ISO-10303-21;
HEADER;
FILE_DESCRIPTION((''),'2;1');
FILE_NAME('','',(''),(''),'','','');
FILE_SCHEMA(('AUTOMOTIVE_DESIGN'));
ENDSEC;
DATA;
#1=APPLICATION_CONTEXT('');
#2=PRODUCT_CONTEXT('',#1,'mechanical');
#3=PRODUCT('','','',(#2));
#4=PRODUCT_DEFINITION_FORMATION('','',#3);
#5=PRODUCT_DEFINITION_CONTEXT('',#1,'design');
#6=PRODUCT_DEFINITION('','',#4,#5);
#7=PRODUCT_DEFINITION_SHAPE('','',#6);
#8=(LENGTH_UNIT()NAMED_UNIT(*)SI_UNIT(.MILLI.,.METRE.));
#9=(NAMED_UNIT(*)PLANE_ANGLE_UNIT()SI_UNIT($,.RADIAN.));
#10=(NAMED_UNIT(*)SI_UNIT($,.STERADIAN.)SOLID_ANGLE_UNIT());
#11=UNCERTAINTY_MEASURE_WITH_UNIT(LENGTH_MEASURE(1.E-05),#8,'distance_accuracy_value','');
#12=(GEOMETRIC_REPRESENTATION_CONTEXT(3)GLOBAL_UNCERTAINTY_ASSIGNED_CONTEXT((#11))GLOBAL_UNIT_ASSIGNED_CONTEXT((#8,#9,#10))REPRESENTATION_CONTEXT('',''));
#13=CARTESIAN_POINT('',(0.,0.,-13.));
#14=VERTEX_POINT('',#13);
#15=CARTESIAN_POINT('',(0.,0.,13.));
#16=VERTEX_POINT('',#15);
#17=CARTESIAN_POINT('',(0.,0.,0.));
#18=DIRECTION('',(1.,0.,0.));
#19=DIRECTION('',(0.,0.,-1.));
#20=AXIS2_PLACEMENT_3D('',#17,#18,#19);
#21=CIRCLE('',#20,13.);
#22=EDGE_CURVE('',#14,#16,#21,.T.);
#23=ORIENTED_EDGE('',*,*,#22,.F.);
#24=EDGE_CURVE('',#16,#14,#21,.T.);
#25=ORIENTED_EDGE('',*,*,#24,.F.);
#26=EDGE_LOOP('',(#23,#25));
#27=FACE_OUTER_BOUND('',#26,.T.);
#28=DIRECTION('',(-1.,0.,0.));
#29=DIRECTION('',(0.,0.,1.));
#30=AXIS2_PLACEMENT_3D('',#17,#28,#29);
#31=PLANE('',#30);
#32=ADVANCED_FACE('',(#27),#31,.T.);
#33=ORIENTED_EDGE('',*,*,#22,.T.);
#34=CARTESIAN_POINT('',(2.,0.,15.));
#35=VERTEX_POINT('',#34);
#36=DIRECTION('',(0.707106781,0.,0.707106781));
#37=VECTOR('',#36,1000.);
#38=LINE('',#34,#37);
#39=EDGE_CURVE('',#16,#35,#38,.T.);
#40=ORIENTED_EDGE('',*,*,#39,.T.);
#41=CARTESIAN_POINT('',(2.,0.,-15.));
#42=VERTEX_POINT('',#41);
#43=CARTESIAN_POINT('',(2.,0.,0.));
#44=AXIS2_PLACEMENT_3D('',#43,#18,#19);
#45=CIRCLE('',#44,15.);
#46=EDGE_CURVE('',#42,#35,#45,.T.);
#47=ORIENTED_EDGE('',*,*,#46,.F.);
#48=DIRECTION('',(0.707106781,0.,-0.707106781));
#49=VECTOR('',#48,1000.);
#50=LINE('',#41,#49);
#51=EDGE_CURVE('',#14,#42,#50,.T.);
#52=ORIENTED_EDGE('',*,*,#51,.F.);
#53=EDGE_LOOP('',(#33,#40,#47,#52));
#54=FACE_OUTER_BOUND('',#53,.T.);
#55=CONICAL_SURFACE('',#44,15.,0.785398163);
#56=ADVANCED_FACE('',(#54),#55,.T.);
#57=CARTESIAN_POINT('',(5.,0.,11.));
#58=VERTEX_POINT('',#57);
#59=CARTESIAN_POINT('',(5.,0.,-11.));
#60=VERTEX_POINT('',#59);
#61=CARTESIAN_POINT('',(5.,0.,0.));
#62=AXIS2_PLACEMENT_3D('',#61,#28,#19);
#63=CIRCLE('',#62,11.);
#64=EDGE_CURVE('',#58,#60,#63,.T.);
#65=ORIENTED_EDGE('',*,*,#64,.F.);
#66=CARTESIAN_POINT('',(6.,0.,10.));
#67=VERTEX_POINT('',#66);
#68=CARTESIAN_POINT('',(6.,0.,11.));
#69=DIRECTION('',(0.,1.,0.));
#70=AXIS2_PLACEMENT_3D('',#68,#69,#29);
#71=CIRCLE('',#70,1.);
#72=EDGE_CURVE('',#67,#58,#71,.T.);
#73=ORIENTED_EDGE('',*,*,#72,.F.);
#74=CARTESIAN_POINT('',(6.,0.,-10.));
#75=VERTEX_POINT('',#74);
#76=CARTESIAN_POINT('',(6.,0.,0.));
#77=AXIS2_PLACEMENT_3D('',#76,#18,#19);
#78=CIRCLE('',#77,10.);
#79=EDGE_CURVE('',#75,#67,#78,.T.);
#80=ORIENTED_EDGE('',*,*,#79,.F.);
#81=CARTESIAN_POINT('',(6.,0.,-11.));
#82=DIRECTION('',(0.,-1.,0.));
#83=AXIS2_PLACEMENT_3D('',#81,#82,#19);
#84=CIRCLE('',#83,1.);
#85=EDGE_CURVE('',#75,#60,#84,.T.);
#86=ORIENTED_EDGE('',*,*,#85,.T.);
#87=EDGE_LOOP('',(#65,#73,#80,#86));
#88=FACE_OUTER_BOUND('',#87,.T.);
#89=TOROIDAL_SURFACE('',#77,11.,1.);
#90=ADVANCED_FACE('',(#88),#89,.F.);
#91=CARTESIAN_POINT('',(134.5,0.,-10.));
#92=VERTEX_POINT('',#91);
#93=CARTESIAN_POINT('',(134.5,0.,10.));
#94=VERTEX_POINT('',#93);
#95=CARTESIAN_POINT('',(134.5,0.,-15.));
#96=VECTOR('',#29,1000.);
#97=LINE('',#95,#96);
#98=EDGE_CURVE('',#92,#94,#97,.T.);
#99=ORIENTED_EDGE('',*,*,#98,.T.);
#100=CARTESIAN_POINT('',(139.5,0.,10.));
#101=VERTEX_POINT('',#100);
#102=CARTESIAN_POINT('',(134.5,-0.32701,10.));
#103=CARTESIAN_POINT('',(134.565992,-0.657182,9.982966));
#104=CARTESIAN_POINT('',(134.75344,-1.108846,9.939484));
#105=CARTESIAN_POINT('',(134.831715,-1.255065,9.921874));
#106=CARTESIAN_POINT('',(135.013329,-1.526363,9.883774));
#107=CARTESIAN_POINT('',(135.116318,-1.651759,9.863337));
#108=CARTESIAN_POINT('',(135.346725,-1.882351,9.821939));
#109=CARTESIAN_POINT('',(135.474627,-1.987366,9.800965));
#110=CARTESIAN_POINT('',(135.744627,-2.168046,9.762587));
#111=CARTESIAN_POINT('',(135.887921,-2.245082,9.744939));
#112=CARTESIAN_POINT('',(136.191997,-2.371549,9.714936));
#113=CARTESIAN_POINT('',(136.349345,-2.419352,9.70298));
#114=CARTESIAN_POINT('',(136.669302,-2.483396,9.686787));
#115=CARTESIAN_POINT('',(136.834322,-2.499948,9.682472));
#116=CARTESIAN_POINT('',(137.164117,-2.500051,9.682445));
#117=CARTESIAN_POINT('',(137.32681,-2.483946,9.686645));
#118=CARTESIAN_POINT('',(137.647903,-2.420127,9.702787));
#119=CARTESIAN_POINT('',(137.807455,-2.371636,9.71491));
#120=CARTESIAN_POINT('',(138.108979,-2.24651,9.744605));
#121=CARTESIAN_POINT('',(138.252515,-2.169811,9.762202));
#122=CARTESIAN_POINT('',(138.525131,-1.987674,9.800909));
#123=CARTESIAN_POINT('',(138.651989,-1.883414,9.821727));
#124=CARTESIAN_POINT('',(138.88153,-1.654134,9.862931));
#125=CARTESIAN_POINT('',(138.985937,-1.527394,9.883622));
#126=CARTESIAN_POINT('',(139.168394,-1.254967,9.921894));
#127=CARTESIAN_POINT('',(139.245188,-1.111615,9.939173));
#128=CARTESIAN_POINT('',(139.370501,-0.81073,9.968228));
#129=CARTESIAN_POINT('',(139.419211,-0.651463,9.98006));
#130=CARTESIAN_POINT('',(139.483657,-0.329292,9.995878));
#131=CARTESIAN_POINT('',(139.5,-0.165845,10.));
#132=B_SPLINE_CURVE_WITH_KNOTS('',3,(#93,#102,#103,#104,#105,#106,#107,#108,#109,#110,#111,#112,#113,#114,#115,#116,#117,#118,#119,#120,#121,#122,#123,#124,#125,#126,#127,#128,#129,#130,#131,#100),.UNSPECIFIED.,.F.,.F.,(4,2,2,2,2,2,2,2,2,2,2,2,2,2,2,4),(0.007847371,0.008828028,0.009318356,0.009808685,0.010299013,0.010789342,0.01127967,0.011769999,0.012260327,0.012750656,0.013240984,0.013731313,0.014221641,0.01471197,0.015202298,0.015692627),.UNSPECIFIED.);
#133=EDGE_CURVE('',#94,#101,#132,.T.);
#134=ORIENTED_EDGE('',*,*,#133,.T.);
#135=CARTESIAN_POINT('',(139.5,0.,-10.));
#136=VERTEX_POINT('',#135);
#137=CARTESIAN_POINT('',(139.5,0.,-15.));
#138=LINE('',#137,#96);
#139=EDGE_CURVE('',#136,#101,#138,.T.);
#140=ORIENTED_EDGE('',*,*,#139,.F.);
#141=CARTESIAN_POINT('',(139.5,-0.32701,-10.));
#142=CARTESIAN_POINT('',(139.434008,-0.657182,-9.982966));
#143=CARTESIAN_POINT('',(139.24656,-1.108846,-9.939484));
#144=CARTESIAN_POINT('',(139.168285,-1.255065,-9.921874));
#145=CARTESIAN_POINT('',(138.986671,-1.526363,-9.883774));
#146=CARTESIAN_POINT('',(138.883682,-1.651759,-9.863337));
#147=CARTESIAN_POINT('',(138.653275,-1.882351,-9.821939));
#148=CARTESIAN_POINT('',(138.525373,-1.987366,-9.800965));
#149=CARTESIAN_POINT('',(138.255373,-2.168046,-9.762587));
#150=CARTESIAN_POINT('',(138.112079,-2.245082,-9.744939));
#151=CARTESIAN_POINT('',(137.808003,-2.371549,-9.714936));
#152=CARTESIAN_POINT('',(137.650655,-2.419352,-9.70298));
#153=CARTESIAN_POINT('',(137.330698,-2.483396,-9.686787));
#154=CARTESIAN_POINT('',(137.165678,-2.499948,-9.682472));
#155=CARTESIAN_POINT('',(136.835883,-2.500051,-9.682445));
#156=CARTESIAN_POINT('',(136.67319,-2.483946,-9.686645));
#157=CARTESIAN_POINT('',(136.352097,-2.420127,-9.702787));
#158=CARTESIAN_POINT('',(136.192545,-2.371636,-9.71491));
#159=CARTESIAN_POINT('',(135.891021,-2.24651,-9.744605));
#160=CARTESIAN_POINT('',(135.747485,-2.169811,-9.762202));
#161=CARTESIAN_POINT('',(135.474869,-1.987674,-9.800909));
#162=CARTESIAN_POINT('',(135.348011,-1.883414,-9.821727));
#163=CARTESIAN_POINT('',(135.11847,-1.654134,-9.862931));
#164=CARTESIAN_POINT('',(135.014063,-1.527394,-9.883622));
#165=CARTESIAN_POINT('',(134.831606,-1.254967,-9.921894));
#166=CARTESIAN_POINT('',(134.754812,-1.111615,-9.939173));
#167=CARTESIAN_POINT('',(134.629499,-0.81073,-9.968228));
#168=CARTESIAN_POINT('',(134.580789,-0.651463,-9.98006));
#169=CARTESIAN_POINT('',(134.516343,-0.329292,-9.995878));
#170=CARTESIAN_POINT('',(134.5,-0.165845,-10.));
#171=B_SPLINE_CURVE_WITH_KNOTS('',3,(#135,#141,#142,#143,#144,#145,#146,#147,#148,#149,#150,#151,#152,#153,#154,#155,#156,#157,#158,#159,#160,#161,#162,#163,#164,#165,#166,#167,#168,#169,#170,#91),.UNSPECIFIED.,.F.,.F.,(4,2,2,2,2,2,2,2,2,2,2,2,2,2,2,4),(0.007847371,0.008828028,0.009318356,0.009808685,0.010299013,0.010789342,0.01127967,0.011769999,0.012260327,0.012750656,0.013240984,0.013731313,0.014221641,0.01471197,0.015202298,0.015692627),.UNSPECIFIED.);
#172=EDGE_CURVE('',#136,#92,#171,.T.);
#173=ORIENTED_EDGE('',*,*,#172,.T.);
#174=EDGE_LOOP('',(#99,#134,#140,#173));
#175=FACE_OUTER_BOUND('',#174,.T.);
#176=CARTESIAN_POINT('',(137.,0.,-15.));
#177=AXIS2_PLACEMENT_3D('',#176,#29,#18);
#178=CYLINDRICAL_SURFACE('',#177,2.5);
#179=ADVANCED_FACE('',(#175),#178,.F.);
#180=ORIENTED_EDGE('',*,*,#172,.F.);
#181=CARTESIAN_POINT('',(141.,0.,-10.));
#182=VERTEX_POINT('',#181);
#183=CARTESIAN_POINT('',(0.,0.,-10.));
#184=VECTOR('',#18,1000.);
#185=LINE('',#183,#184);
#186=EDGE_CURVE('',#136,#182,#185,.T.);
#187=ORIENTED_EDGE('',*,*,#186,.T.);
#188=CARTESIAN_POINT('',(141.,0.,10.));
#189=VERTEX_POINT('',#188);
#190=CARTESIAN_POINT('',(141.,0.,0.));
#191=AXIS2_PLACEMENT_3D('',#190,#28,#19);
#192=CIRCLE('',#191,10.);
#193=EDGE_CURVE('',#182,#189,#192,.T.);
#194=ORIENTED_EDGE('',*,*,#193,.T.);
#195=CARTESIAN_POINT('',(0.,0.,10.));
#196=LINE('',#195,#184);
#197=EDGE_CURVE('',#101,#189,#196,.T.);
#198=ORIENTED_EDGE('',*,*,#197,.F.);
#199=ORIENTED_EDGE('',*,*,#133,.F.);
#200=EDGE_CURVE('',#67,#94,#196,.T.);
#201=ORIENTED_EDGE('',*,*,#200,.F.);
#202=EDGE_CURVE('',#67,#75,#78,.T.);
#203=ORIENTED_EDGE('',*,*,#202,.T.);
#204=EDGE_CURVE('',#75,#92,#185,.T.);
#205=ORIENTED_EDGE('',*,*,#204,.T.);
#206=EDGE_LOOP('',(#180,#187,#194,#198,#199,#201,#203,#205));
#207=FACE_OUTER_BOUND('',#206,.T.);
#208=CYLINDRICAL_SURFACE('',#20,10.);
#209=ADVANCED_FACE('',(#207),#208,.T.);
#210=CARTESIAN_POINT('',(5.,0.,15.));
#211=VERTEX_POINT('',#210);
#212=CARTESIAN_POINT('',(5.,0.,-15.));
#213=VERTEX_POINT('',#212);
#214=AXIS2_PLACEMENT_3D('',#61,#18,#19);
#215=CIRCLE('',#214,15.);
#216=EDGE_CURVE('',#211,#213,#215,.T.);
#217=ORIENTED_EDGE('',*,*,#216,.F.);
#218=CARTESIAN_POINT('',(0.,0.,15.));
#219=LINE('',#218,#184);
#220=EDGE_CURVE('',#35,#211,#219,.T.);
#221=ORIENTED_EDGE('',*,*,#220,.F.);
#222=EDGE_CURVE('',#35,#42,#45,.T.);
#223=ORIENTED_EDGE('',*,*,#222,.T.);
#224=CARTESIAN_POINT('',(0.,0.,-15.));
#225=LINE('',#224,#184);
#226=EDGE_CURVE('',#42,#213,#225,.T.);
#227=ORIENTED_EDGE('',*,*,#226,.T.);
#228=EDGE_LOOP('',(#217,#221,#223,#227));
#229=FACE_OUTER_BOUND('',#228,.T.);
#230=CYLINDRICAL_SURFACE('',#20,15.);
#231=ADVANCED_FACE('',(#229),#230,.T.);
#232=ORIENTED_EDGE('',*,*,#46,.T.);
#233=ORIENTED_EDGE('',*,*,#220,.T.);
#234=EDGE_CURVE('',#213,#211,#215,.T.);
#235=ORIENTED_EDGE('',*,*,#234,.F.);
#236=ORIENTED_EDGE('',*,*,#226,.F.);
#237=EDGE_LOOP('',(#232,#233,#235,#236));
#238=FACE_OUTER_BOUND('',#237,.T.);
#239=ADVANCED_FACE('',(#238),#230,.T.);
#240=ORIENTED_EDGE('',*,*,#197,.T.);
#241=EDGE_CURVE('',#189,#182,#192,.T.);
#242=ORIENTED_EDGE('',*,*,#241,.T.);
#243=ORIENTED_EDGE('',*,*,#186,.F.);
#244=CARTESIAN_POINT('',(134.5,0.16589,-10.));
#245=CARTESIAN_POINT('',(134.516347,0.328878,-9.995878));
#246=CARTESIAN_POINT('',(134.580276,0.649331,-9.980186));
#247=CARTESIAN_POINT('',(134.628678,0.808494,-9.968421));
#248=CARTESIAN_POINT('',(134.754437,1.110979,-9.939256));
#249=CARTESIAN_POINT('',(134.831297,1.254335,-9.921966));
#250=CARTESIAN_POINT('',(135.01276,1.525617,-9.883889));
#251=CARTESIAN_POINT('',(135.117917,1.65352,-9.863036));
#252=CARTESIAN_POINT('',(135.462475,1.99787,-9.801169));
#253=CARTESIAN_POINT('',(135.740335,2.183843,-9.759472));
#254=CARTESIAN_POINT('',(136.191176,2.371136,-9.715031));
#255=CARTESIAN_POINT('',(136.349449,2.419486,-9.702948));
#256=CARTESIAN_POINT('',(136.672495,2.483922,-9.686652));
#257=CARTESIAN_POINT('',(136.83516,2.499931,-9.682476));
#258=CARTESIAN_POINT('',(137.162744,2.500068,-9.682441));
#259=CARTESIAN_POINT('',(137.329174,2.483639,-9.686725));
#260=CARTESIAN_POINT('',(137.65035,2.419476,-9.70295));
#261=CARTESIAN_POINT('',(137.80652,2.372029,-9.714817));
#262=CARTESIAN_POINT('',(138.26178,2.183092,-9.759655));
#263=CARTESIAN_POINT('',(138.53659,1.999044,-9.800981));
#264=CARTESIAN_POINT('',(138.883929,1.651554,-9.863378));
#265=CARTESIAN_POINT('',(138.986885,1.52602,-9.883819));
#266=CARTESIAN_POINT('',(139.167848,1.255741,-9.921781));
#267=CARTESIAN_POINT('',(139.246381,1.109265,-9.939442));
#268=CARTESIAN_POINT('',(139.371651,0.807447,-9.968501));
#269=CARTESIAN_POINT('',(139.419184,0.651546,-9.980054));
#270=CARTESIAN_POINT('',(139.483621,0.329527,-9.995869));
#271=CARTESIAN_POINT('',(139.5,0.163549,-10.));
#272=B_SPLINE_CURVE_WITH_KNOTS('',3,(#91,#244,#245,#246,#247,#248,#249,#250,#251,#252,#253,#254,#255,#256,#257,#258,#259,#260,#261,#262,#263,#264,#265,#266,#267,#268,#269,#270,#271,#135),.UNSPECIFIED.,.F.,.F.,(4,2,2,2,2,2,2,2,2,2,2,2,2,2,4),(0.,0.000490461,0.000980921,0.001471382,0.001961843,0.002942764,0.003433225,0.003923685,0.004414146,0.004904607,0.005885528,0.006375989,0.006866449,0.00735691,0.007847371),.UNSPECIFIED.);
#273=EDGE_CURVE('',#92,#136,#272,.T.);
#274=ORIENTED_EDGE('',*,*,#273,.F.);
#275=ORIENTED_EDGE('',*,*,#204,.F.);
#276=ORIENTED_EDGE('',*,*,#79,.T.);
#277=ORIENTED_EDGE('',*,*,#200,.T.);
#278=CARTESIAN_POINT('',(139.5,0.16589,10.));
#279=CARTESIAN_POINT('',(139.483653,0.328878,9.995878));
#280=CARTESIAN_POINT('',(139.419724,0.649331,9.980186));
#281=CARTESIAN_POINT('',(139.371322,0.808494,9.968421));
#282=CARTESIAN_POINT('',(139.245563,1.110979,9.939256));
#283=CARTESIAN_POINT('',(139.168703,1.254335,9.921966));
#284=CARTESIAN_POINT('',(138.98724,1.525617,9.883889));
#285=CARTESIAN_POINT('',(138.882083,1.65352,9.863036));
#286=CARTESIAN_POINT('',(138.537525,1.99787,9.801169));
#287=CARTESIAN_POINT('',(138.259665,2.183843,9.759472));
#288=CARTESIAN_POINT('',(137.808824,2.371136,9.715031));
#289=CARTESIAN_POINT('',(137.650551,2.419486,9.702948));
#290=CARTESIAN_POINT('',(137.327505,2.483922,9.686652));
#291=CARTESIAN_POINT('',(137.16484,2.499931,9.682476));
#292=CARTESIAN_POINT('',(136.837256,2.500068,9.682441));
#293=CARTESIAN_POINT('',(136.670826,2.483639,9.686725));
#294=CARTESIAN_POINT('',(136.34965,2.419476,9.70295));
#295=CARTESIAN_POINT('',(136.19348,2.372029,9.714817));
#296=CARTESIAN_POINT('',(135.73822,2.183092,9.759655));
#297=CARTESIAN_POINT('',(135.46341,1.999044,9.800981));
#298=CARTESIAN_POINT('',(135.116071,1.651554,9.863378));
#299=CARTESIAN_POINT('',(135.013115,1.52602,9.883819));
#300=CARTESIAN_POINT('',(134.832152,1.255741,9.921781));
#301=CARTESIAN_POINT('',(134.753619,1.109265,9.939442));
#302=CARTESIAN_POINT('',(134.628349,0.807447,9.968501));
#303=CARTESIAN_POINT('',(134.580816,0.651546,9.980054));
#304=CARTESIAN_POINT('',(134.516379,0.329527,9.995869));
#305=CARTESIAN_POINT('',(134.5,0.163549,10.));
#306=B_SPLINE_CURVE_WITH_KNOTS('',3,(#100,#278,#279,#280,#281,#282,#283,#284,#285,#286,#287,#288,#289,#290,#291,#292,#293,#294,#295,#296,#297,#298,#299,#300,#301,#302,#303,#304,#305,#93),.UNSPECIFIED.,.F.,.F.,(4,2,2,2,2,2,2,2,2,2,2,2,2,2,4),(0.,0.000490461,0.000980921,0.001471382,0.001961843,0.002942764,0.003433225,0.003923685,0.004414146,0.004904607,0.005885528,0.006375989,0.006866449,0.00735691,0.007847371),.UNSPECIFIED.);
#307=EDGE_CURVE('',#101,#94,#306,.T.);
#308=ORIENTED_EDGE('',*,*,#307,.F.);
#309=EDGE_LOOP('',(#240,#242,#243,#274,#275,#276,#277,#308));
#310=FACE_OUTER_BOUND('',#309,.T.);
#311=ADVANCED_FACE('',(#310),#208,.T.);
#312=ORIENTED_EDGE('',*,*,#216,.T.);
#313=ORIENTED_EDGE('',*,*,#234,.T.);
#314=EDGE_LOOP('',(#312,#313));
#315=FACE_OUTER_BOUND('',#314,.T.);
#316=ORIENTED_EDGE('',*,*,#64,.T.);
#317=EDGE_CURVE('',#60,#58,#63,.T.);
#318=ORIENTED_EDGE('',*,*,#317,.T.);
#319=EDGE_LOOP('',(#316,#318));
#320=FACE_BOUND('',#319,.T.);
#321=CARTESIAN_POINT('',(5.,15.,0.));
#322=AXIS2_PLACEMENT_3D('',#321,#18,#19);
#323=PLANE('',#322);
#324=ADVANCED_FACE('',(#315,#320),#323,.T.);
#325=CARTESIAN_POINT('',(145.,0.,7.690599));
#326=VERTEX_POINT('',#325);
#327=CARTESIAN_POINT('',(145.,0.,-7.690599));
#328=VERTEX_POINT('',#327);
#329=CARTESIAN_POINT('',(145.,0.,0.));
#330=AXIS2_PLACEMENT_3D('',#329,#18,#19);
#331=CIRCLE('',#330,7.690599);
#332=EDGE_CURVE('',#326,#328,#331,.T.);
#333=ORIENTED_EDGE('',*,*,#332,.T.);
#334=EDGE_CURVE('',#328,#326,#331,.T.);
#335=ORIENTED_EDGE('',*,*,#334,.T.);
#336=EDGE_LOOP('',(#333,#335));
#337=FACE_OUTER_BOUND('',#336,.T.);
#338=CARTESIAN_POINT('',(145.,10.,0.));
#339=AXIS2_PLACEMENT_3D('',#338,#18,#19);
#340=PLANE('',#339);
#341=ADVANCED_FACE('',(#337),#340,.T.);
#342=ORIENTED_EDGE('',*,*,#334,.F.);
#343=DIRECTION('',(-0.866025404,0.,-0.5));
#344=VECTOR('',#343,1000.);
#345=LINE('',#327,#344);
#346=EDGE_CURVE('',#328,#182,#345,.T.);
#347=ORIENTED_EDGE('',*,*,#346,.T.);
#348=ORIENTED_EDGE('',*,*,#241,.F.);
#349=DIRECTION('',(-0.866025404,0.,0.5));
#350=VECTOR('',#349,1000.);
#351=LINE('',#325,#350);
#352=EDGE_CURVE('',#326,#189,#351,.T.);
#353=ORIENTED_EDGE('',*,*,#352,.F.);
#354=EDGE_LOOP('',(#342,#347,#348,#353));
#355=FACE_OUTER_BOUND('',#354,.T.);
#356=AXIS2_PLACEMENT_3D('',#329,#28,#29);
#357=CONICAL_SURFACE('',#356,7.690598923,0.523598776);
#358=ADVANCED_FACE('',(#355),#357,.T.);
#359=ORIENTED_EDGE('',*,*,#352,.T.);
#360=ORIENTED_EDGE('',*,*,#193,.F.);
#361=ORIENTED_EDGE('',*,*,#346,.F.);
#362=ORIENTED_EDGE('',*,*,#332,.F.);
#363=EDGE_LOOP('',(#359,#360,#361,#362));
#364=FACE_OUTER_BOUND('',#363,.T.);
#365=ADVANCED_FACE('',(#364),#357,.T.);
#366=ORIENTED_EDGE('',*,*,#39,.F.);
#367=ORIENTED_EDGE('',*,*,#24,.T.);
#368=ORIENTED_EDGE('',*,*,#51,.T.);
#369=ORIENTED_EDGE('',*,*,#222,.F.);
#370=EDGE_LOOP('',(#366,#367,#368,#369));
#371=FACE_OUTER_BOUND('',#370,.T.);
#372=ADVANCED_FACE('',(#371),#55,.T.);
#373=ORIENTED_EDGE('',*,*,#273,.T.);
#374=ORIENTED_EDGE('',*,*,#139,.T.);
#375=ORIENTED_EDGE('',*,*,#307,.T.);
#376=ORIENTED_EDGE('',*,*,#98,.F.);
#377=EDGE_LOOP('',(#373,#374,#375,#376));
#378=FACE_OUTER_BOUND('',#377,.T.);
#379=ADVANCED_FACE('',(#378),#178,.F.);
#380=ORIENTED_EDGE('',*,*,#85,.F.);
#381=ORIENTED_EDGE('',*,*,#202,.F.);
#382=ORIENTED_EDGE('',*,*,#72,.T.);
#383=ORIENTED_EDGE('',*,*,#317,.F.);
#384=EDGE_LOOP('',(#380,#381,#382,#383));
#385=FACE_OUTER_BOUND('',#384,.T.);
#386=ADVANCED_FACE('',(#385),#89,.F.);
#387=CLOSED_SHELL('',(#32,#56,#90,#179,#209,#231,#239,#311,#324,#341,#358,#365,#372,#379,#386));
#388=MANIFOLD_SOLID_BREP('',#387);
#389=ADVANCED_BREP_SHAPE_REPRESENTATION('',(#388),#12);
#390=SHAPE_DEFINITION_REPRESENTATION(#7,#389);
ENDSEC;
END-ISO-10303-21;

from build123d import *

# Parameters (mm, degrees)
CUT_EXTRUDE1_DEPTH      = 147.543508898
CUT_EXTRUDE1_DEPTH_BACK = 147.543508898
SKETCH2_R               = 2.5
FILLET1_R               = 1
CHAMFER1_SIZE           = 4
CHAMFER1_SIZE2          = 2.309401077


with BuildPart() as part:
    # Sketch1 → Base-Revolve (revolve)
    with BuildSketch(Plane.XY, mode=Mode.PRIVATE) as base_revolve_sk:
        Polygon((0, 0), (145, 0), (145, 10), (5, 10), (5, 15), (2, 15), (0, 13), align=None)
    revolve(base_revolve_sk.sketch.rotate(Axis((0, 0, 0), (-1, 0, 0)), 90), axis=Axis((0, 0, 0), (-1, 0, 0)))

    # Sketch2 → Cut-Extrude1 (cut, two sides: drawn at the far end of the back side and taken through both)
    with BuildSketch(Plane.XY.offset(-CUT_EXTRUDE1_DEPTH_BACK)):
        with Locations((137, 0)):
            Circle(SKETCH2_R)
    extrude(amount=CUT_EXTRUDE1_DEPTH + CUT_EXTRUDE1_DEPTH_BACK, mode=Mode.SUBTRACT)

    # Fillet1
    fillet1_edges = [part.edges().sort_by_distance(p)[0] for p in [
        (5, 0, 10),
    ]]
    fillet(fillet1_edges, radius=FILLET1_R)

    # Chamfer1
    chamfer1_edges = [part.edges().sort_by_distance(p)[0] for p in [
        (145, 0, 10),
    ]]
    chamfer1_side = [part.faces().sort_by_distance(p)[0] for p in [
        (75.5, 0, 10),
    ]]
    chamfer(chamfer1_edges, length=CHAMFER1_SIZE, length2=CHAMFER1_SIZE2, reference=chamfer1_side[0])


solid = part.part
